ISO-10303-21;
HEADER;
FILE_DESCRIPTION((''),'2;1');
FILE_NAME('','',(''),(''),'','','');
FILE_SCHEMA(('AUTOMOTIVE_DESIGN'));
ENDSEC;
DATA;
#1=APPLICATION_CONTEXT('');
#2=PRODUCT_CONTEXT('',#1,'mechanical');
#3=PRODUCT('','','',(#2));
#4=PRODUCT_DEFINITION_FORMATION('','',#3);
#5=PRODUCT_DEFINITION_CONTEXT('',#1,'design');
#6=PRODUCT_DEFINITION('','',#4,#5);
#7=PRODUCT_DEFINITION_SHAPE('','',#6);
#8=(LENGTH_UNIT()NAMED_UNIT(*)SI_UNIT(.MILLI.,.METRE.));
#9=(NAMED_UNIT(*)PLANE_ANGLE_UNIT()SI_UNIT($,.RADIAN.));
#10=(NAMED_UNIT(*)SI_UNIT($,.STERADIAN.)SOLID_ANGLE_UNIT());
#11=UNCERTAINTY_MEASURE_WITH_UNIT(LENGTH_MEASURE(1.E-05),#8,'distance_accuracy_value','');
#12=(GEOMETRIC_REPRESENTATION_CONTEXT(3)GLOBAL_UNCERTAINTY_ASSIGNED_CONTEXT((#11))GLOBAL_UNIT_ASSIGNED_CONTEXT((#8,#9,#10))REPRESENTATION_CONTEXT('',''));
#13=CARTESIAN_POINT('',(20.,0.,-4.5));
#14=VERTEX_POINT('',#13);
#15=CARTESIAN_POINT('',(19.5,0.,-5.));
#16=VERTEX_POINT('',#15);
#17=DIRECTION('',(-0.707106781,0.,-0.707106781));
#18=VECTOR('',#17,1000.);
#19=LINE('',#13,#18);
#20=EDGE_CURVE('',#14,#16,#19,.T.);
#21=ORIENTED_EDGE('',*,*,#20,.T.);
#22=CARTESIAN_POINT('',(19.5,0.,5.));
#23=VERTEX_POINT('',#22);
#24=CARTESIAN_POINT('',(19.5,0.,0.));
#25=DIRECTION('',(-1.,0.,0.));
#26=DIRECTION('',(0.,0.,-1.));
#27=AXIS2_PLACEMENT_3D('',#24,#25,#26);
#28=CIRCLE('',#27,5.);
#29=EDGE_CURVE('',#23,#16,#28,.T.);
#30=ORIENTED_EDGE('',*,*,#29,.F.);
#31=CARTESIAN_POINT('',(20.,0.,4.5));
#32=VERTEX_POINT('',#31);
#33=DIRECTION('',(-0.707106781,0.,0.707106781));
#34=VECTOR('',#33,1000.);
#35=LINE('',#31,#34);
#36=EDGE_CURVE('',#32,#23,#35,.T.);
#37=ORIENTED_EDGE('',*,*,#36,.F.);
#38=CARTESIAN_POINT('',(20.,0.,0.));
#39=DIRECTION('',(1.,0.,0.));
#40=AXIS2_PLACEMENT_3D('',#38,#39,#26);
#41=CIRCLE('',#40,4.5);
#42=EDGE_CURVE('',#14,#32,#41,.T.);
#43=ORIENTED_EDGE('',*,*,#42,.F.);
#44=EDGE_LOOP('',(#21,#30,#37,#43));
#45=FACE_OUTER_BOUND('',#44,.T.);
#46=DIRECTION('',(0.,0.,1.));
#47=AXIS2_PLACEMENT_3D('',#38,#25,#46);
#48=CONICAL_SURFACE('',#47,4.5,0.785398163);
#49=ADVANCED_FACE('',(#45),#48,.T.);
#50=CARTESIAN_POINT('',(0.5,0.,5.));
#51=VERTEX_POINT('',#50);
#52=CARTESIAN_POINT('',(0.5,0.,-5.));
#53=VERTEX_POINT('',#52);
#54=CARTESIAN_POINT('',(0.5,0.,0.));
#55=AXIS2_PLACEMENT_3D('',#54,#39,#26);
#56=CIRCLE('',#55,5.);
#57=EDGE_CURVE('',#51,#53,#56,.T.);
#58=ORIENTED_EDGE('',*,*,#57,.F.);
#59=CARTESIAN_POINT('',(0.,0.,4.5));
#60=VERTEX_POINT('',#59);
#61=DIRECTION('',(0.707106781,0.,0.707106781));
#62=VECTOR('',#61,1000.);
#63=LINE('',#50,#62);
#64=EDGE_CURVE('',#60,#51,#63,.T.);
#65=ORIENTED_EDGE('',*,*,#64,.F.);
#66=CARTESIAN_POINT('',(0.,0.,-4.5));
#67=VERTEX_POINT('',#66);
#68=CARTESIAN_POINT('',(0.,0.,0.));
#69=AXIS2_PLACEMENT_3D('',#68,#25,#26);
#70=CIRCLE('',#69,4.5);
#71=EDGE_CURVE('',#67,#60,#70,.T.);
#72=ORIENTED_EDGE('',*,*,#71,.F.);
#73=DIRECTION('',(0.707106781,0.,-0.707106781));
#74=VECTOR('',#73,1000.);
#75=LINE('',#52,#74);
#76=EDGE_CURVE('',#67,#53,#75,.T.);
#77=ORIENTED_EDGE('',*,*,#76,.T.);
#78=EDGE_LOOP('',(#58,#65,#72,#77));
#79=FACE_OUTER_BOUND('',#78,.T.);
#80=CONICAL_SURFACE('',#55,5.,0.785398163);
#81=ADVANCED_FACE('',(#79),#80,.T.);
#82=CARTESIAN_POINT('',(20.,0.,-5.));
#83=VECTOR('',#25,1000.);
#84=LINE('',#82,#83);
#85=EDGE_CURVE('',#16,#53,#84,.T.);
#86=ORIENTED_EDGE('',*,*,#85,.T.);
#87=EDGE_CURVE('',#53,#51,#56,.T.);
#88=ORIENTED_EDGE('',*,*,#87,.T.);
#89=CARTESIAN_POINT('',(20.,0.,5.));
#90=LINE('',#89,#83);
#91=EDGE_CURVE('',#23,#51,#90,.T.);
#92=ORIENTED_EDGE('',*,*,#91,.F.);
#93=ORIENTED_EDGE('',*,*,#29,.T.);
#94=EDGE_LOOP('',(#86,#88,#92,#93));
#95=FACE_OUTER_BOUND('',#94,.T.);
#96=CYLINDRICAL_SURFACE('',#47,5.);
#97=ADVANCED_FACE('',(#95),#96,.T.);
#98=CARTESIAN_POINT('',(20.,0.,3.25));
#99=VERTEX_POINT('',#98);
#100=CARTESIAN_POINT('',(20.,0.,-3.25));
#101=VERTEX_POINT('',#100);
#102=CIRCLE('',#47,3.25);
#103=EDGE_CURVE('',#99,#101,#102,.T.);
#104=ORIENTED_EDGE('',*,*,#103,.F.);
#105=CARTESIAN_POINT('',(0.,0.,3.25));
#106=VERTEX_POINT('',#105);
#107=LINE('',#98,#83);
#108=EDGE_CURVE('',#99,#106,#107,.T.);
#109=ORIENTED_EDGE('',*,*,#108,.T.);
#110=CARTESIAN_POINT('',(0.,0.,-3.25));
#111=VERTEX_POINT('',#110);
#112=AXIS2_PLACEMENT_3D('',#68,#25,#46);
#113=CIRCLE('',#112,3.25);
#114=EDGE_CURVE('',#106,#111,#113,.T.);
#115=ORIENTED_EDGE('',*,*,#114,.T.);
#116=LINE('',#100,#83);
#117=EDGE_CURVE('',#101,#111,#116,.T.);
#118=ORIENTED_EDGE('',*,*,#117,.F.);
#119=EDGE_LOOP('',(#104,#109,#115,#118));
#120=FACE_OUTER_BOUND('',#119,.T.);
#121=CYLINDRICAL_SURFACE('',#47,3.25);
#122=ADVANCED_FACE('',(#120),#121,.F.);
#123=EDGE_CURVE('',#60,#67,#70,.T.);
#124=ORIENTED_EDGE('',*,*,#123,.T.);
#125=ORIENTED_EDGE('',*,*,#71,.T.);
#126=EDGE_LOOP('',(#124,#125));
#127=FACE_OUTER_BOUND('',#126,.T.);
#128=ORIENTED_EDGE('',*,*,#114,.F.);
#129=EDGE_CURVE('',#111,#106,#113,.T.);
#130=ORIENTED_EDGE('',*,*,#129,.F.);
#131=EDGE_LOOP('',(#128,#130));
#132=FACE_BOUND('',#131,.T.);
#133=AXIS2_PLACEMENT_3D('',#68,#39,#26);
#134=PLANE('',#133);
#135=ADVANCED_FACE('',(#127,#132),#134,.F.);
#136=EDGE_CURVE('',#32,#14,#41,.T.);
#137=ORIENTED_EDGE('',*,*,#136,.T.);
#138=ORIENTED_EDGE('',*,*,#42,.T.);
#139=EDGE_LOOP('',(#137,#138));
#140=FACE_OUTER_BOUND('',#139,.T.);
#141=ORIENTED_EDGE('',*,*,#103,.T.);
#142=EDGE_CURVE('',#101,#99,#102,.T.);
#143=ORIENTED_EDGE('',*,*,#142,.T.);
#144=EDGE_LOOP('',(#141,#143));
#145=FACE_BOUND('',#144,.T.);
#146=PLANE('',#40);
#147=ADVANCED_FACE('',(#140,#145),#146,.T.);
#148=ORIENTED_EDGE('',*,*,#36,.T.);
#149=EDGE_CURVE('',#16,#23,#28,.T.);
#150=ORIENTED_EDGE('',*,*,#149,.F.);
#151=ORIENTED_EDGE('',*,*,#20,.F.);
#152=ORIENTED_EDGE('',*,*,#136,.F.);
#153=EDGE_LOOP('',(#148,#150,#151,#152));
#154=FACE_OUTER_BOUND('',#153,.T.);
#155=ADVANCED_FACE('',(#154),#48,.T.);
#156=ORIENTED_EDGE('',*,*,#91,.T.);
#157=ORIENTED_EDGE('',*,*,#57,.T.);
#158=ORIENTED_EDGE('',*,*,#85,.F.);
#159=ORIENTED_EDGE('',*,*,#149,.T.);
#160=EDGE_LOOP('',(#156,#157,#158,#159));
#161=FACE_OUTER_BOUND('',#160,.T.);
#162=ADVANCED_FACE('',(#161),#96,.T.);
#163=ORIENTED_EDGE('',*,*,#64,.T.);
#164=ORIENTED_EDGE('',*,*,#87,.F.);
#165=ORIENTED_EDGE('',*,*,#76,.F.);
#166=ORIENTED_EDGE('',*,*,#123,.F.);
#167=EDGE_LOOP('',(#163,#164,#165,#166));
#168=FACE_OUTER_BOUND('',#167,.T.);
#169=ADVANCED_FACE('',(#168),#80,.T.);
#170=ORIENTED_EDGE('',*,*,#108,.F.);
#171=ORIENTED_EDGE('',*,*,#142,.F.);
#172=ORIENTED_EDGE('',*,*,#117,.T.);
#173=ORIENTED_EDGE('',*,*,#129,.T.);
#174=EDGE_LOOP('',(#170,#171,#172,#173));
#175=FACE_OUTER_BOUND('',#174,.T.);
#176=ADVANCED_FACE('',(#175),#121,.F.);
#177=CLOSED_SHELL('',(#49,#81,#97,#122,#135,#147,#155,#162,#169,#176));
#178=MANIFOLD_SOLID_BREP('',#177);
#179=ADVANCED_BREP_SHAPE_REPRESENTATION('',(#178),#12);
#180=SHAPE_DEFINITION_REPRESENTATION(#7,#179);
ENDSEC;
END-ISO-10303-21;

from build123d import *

# Parameters (mm, degrees)
SKETCH_1_R          = 5
EXTRUDE_1_DEPTH     = 20
CHAMFER_1_SIZE      = 0.5
SKETCH_2_R          = 3.25
CUT_EXTRUDE_1_DEPTH = 22.213203436


with BuildPart() as part:
    # 草图1 → 凸台-拉伸1 (new body)
    with BuildSketch(Plane(origin=(0, 0, 0), x_dir=(0, 0, -1), z_dir=(1, 0, 0))):
        Circle(SKETCH_1_R)
    extrude(amount=EXTRUDE_1_DEPTH)

    # 倒角1
    chamfer_1_edges = [part.edges().sort_by_distance(p)[0] for p in [
        (0, 0, 5),
        (20, 0, 5),
    ]]
    chamfer(chamfer_1_edges, length=CHAMFER_1_SIZE)

    # 草图2 → 切除-拉伸1 (cut, through all)
    with BuildSketch(Plane.ZY):
        Circle(SKETCH_2_R)
    extrude(amount=-CUT_EXTRUDE_1_DEPTH, mode=Mode.SUBTRACT)


solid = part.part
